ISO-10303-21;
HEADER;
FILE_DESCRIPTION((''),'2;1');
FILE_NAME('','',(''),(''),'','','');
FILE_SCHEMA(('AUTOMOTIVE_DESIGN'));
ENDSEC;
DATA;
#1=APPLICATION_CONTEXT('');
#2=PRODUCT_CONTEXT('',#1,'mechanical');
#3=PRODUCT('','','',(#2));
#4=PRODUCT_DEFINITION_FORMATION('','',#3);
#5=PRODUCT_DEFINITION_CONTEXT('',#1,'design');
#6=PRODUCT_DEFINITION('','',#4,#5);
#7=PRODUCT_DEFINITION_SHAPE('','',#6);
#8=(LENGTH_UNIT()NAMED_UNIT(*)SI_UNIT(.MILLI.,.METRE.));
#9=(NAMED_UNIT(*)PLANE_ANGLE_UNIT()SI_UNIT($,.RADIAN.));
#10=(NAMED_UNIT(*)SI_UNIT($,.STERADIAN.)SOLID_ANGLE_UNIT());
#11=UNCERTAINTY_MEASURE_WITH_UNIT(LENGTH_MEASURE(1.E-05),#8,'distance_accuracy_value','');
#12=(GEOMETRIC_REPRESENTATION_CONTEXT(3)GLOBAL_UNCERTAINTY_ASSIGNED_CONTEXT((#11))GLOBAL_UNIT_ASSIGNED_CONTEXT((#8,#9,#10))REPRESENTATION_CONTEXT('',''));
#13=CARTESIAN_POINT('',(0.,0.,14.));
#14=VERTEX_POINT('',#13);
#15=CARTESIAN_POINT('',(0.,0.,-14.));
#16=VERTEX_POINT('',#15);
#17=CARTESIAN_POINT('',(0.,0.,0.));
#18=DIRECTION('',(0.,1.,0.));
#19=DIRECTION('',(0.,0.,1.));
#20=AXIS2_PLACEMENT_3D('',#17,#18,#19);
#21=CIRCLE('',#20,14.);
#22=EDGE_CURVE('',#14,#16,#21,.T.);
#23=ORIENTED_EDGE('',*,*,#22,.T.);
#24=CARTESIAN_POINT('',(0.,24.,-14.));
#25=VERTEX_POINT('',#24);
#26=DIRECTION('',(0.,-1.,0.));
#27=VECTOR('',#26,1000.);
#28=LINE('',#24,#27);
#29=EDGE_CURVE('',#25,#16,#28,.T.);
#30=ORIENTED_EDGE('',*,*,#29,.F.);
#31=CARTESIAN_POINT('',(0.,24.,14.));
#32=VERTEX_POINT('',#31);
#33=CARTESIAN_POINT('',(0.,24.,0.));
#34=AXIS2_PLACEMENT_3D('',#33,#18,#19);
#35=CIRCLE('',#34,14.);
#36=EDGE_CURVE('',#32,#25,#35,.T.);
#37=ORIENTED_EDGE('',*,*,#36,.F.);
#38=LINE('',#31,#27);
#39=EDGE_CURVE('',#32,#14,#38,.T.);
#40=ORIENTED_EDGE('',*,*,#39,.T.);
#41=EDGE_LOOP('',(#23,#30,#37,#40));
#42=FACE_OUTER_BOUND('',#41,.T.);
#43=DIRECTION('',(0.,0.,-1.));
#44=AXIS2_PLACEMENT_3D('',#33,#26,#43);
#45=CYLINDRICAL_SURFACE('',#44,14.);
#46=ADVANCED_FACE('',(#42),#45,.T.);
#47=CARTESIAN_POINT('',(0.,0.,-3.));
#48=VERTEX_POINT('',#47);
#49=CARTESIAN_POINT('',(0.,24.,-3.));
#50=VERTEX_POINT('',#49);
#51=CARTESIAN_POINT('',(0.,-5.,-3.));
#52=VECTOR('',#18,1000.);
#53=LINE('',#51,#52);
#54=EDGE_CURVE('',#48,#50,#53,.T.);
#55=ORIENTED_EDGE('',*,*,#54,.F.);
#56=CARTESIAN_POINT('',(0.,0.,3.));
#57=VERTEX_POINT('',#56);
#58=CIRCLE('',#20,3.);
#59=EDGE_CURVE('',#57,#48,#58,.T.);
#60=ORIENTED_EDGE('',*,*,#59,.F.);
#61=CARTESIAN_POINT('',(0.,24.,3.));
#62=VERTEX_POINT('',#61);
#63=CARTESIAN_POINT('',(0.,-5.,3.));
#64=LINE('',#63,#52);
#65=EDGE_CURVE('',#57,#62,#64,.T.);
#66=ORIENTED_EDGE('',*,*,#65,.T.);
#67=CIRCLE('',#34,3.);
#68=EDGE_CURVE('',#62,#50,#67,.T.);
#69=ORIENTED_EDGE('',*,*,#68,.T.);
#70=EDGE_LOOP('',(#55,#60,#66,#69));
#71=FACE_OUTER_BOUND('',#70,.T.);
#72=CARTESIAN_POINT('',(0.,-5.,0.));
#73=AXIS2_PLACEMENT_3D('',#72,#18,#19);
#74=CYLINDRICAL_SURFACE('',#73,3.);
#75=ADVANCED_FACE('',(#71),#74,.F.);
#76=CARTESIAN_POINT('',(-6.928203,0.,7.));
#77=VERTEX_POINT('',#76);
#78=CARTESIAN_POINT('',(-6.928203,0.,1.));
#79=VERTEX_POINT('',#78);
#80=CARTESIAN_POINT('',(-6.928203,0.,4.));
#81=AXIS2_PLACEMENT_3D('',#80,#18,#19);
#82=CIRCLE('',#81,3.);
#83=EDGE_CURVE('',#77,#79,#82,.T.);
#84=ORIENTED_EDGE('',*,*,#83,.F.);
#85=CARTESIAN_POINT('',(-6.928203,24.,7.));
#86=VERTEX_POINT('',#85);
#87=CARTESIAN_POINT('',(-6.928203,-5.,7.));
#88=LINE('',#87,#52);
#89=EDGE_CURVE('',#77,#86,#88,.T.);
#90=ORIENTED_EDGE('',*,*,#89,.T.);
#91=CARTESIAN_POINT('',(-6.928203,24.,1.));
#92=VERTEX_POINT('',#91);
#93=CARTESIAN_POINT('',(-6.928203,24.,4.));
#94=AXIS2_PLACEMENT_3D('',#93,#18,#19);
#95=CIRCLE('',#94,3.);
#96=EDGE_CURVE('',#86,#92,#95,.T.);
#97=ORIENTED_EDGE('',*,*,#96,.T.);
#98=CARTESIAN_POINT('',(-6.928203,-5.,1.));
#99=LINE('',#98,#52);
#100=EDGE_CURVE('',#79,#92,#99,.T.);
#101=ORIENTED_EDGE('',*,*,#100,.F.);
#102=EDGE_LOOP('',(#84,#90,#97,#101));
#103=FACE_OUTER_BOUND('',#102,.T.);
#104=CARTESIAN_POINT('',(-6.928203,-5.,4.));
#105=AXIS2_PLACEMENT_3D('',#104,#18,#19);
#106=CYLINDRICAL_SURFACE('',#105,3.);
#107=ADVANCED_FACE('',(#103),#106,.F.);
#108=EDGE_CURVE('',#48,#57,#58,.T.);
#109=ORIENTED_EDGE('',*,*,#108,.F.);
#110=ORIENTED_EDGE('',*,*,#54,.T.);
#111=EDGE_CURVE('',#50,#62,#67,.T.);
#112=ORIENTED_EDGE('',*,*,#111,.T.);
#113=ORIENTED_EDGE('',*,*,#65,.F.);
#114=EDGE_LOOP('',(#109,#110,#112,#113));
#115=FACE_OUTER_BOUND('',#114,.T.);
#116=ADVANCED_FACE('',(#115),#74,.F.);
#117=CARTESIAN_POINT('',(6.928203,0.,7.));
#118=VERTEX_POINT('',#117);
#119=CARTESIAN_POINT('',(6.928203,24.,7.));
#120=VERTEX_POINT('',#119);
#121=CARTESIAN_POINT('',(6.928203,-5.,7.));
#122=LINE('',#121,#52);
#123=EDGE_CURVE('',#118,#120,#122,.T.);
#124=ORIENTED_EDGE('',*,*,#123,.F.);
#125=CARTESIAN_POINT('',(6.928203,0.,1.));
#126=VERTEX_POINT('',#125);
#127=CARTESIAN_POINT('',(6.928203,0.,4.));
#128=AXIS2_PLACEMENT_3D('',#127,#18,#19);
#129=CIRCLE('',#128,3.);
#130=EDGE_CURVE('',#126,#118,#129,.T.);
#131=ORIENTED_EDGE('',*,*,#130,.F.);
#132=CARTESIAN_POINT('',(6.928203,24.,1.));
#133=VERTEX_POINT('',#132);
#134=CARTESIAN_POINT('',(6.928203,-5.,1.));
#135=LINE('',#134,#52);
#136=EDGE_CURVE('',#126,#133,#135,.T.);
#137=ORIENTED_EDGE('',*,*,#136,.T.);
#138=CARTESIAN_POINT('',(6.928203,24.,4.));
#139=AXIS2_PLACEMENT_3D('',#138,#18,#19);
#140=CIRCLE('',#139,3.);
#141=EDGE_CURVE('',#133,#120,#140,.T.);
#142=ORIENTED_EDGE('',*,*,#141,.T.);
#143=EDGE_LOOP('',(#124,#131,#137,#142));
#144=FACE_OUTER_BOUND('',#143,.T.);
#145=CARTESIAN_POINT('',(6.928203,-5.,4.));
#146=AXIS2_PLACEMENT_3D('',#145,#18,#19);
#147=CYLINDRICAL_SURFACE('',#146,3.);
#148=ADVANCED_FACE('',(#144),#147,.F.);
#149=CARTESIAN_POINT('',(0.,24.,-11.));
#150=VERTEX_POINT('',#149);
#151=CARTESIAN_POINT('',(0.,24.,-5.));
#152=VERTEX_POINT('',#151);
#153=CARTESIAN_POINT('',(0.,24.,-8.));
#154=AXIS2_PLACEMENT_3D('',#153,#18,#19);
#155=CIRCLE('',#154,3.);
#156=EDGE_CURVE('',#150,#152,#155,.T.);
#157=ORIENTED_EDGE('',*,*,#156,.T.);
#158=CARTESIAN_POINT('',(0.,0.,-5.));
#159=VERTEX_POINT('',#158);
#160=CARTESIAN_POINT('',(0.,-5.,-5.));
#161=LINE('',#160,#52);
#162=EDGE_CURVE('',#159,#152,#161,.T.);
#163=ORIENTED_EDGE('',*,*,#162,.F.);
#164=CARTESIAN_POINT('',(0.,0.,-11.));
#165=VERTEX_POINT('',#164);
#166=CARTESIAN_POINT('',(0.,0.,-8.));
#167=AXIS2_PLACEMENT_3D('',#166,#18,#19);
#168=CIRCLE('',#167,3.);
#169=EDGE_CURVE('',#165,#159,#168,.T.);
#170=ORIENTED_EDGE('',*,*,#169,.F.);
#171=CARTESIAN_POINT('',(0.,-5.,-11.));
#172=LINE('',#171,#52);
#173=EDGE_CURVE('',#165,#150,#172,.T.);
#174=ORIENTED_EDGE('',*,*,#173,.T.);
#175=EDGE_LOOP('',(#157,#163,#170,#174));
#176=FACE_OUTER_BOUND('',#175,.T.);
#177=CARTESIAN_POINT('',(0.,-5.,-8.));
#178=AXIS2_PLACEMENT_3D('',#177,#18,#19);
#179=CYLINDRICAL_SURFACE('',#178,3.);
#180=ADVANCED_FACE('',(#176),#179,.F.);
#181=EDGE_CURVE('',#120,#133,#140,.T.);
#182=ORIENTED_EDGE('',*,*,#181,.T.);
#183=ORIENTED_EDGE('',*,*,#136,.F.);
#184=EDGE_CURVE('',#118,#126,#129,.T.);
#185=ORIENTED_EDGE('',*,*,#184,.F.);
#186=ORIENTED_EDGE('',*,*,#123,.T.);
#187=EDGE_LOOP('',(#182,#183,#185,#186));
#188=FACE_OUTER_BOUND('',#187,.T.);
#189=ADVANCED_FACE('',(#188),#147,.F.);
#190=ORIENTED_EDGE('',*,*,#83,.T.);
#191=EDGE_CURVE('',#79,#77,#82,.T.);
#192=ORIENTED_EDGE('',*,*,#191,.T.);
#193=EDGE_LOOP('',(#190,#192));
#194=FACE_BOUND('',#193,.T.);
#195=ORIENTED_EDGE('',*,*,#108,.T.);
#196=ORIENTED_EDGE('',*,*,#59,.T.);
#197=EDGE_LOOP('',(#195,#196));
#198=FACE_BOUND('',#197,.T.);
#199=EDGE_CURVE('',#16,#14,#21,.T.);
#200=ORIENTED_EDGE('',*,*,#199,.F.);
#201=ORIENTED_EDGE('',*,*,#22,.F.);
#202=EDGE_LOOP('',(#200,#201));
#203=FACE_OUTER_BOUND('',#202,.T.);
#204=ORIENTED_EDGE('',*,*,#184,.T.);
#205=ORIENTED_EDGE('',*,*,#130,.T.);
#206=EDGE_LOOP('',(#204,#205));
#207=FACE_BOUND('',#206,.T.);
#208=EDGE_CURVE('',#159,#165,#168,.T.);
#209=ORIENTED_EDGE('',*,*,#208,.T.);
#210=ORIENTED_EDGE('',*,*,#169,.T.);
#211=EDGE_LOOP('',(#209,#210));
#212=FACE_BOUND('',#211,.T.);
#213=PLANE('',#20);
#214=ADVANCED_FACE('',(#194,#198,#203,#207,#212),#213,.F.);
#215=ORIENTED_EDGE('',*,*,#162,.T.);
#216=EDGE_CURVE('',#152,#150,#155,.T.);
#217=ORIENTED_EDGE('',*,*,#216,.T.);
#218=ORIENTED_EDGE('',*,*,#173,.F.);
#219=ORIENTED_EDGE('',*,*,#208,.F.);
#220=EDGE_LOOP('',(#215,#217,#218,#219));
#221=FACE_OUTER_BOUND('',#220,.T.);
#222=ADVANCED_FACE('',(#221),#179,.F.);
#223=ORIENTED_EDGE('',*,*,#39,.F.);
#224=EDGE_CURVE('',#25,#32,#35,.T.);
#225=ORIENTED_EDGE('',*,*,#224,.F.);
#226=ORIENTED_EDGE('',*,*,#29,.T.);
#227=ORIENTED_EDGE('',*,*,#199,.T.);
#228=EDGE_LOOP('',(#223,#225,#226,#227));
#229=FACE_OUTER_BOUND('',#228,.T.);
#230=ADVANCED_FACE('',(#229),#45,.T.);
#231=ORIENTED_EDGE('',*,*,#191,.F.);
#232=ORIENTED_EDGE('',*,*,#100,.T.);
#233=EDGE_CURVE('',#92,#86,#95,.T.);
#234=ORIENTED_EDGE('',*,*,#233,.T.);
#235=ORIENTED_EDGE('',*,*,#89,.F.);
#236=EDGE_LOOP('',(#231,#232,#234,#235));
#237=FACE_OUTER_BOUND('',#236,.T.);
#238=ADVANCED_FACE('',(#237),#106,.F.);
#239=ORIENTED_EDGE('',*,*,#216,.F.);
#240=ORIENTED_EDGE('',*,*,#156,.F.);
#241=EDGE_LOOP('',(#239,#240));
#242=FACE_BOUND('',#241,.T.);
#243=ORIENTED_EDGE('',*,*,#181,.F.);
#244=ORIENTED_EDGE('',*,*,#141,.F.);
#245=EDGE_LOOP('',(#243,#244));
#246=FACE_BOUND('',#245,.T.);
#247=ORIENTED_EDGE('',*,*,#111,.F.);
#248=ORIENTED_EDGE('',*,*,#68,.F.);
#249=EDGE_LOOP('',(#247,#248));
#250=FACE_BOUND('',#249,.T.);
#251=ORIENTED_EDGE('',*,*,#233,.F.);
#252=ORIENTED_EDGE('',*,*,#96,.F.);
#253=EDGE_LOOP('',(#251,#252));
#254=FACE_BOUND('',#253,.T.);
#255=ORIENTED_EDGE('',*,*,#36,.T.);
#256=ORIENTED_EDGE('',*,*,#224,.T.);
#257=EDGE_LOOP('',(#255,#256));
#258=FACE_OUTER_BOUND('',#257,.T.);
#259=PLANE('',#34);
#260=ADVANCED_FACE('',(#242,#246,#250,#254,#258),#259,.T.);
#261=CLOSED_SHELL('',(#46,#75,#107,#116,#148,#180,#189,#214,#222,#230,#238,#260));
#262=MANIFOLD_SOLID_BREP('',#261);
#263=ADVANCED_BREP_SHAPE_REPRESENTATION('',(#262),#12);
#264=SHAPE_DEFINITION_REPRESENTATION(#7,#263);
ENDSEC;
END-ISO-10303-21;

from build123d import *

# Parameters (mm, degrees)
CYLINDER_PROFILE_28_R           = 14
CYLINDER_BODY_28X24_DEPTH       = 24
HOLE_CIRCLE_SKETCH_3X_6_PCD16_R = 3
THROUGH_HOLES_3X_6_PCD16_DEPTH  = 29
CENTRE_HOLE_SKETCH_6_R          = 3
CENTRE_HOLE_6_DEPTH             = 29


with BuildPart() as part:
    # Cylinder Profile Ø28 → Cylinder Body Ø28x24 (new body)
    with BuildSketch(Plane(origin=(0, 0, 0), x_dir=(1, 0, 0), z_dir=(0, 1, 0))):
        with Locations(Location((0, 0, 0), (0, 0, 270))):
            Circle(CYLINDER_PROFILE_28_R)
    extrude(amount=CYLINDER_BODY_28X24_DEPTH)

    # Hole Circle Sketch 3xØ6 PCD16 → Through Holes 3xØ6 PCD16 (cut)
    with BuildSketch(Plane(origin=(0, 24, 0), x_dir=(1, 0, 0), z_dir=(0, 1, 0))):
        with Locations(Location((0, 8, 0), (0, 0, 270))):
            Circle(HOLE_CIRCLE_SKETCH_3X_6_PCD16_R)
        with Locations(Location((6.92820323, -4, 0), (0, 0, 270))):
            Circle(HOLE_CIRCLE_SKETCH_3X_6_PCD16_R)
        with Locations(Location((-6.92820323, -4, 0), (0, 0, 270))):
            Circle(HOLE_CIRCLE_SKETCH_3X_6_PCD16_R)
    extrude(amount=-THROUGH_HOLES_3X_6_PCD16_DEPTH, mode=Mode.SUBTRACT)

    # Centre Hole Sketch Ø6 → Centre Hole Ø6 (cut)
    with BuildSketch(Plane(origin=(0, 24, 0), x_dir=(1, 0, 0), z_dir=(0, 1, 0))):
        with Locations(Location((0, 0, 0), (0, 0, 270))):
            Circle(CENTRE_HOLE_SKETCH_6_R)
    extrude(amount=-CENTRE_HOLE_6_DEPTH, mode=Mode.SUBTRACT)


solid = part.part
